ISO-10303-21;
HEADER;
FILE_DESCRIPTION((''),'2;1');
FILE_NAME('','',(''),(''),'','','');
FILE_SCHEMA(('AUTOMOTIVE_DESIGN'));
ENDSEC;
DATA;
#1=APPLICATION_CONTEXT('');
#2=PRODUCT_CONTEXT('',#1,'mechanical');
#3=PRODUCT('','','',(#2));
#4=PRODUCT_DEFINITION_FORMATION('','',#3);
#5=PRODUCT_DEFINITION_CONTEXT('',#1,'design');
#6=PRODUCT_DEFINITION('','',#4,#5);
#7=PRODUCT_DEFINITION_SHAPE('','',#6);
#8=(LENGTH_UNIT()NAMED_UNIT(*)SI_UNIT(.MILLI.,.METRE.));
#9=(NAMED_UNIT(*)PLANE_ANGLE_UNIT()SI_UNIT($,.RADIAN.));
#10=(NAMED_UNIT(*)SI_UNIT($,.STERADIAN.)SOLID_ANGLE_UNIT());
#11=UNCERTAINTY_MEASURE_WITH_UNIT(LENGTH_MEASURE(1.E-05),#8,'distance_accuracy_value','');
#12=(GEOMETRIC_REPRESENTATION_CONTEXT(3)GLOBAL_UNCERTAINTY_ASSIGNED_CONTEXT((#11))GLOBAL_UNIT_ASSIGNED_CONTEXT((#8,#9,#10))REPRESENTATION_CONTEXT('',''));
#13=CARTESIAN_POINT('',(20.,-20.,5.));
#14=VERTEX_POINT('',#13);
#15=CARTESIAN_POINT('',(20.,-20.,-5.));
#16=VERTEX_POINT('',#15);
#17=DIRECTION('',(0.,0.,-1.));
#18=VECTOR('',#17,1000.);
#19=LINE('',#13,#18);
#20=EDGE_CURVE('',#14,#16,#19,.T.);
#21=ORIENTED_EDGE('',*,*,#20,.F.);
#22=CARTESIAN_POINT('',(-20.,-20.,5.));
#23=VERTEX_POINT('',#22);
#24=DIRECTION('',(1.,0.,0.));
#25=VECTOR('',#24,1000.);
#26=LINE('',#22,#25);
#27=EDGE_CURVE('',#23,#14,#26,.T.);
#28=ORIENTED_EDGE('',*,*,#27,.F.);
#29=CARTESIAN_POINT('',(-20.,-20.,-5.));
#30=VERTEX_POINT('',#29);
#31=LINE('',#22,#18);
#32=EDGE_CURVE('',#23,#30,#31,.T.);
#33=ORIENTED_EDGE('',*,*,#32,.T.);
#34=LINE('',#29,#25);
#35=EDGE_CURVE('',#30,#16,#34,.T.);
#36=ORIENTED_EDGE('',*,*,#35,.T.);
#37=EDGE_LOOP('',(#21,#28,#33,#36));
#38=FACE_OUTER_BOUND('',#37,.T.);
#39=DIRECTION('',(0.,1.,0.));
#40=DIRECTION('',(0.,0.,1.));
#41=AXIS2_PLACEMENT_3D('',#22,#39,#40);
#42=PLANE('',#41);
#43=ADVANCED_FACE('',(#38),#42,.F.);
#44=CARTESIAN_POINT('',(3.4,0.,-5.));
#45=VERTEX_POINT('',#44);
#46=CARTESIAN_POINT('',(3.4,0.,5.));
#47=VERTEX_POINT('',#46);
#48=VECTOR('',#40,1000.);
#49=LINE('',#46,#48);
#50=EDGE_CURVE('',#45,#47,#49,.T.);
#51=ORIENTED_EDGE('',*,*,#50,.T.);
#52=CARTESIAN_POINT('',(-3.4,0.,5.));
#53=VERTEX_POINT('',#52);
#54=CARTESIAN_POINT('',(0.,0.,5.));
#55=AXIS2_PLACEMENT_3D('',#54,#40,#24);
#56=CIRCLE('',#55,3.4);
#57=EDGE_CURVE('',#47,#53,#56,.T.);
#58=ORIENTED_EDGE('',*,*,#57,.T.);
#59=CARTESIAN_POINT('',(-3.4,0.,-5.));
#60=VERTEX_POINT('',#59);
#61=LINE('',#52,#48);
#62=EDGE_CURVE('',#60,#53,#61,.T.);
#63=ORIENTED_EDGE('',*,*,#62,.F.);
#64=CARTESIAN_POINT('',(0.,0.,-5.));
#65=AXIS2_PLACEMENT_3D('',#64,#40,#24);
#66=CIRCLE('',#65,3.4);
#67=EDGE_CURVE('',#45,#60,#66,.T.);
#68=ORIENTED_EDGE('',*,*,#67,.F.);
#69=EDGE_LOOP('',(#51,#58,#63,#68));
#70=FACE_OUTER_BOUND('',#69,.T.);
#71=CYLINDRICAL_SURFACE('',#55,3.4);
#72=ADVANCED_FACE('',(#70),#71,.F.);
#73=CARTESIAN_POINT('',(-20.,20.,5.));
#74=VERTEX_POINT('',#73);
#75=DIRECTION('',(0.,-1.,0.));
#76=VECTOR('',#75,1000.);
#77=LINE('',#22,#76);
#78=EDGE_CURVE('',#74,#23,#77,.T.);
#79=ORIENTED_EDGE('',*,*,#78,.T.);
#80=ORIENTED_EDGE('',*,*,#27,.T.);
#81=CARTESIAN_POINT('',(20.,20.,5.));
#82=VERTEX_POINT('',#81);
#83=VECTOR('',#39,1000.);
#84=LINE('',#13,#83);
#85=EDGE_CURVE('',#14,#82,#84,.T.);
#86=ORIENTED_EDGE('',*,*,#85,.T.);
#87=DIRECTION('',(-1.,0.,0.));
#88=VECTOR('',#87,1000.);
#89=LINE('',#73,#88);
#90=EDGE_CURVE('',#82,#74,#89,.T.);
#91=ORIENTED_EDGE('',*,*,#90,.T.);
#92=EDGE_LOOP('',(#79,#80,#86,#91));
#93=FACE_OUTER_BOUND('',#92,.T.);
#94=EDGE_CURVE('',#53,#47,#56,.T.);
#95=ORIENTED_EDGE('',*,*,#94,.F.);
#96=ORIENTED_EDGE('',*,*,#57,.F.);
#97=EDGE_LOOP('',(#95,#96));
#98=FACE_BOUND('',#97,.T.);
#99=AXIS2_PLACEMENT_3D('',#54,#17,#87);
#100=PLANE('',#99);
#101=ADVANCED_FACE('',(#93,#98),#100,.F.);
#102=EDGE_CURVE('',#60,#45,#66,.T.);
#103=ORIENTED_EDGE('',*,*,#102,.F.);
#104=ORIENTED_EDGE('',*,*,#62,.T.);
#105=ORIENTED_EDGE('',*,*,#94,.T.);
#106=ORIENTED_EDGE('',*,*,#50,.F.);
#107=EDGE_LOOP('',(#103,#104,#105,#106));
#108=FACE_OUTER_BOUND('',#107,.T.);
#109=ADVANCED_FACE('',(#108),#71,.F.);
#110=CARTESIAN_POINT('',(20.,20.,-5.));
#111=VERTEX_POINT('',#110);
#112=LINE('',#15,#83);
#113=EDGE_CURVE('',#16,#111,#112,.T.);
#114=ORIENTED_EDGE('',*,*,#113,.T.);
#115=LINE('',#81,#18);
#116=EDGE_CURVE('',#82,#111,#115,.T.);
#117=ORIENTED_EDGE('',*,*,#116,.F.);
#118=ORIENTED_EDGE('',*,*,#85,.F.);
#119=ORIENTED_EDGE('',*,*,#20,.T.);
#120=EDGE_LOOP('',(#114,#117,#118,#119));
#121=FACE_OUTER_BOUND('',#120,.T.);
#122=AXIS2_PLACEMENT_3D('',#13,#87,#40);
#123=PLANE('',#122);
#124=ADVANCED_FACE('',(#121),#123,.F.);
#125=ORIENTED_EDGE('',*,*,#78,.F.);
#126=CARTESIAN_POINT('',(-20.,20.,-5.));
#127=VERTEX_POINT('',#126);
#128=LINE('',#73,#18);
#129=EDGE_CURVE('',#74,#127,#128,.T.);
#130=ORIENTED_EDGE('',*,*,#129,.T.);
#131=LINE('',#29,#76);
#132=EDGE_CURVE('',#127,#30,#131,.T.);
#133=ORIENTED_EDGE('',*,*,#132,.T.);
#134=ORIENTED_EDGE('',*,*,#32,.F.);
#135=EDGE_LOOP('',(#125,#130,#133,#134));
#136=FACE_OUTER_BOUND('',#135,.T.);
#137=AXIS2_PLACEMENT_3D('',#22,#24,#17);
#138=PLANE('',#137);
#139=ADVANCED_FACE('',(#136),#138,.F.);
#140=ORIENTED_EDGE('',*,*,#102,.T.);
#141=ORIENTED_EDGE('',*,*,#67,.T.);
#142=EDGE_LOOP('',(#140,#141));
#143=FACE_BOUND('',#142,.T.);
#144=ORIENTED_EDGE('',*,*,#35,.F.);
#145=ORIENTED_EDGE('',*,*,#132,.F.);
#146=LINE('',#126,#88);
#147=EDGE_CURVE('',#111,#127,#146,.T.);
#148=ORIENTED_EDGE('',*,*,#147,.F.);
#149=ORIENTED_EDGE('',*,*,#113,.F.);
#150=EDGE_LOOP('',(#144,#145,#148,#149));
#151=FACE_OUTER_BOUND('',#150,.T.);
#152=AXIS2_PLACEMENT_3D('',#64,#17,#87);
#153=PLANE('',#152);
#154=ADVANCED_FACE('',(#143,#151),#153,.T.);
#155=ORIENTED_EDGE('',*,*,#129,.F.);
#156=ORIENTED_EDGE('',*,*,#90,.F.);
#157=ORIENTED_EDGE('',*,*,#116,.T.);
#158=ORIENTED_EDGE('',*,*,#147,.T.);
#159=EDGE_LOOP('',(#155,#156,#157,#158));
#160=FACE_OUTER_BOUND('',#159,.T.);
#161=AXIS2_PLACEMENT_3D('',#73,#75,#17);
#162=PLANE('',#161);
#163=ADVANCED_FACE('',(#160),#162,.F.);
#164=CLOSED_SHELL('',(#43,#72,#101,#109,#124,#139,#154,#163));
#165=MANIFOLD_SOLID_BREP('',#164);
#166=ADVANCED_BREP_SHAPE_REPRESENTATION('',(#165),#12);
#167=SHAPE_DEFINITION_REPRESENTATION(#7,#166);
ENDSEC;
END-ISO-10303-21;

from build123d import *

# Parameters (mm, degrees)
SKETCH_1_W         = 40
SKETCH_1_H         = 40
EXTRUDE_1_DEPTH    = 5
HOLE_WIZARD_M8_1_D = 6.8


with BuildPart() as part:
    # 草图1 → 凸台-拉伸1 (new, symmetric)
    with BuildSketch(Plane.XY):
        Rectangle(SKETCH_1_W, SKETCH_1_H)
    extrude(amount=EXTRUDE_1_DEPTH, both=True)

    # M8 螺纹孔1 (through all)
    with Locations(Plane.XY.offset(5)):
        with Locations((0, 0)):
            Hole(HOLE_WIZARD_M8_1_D / 2)


solid = part.part
